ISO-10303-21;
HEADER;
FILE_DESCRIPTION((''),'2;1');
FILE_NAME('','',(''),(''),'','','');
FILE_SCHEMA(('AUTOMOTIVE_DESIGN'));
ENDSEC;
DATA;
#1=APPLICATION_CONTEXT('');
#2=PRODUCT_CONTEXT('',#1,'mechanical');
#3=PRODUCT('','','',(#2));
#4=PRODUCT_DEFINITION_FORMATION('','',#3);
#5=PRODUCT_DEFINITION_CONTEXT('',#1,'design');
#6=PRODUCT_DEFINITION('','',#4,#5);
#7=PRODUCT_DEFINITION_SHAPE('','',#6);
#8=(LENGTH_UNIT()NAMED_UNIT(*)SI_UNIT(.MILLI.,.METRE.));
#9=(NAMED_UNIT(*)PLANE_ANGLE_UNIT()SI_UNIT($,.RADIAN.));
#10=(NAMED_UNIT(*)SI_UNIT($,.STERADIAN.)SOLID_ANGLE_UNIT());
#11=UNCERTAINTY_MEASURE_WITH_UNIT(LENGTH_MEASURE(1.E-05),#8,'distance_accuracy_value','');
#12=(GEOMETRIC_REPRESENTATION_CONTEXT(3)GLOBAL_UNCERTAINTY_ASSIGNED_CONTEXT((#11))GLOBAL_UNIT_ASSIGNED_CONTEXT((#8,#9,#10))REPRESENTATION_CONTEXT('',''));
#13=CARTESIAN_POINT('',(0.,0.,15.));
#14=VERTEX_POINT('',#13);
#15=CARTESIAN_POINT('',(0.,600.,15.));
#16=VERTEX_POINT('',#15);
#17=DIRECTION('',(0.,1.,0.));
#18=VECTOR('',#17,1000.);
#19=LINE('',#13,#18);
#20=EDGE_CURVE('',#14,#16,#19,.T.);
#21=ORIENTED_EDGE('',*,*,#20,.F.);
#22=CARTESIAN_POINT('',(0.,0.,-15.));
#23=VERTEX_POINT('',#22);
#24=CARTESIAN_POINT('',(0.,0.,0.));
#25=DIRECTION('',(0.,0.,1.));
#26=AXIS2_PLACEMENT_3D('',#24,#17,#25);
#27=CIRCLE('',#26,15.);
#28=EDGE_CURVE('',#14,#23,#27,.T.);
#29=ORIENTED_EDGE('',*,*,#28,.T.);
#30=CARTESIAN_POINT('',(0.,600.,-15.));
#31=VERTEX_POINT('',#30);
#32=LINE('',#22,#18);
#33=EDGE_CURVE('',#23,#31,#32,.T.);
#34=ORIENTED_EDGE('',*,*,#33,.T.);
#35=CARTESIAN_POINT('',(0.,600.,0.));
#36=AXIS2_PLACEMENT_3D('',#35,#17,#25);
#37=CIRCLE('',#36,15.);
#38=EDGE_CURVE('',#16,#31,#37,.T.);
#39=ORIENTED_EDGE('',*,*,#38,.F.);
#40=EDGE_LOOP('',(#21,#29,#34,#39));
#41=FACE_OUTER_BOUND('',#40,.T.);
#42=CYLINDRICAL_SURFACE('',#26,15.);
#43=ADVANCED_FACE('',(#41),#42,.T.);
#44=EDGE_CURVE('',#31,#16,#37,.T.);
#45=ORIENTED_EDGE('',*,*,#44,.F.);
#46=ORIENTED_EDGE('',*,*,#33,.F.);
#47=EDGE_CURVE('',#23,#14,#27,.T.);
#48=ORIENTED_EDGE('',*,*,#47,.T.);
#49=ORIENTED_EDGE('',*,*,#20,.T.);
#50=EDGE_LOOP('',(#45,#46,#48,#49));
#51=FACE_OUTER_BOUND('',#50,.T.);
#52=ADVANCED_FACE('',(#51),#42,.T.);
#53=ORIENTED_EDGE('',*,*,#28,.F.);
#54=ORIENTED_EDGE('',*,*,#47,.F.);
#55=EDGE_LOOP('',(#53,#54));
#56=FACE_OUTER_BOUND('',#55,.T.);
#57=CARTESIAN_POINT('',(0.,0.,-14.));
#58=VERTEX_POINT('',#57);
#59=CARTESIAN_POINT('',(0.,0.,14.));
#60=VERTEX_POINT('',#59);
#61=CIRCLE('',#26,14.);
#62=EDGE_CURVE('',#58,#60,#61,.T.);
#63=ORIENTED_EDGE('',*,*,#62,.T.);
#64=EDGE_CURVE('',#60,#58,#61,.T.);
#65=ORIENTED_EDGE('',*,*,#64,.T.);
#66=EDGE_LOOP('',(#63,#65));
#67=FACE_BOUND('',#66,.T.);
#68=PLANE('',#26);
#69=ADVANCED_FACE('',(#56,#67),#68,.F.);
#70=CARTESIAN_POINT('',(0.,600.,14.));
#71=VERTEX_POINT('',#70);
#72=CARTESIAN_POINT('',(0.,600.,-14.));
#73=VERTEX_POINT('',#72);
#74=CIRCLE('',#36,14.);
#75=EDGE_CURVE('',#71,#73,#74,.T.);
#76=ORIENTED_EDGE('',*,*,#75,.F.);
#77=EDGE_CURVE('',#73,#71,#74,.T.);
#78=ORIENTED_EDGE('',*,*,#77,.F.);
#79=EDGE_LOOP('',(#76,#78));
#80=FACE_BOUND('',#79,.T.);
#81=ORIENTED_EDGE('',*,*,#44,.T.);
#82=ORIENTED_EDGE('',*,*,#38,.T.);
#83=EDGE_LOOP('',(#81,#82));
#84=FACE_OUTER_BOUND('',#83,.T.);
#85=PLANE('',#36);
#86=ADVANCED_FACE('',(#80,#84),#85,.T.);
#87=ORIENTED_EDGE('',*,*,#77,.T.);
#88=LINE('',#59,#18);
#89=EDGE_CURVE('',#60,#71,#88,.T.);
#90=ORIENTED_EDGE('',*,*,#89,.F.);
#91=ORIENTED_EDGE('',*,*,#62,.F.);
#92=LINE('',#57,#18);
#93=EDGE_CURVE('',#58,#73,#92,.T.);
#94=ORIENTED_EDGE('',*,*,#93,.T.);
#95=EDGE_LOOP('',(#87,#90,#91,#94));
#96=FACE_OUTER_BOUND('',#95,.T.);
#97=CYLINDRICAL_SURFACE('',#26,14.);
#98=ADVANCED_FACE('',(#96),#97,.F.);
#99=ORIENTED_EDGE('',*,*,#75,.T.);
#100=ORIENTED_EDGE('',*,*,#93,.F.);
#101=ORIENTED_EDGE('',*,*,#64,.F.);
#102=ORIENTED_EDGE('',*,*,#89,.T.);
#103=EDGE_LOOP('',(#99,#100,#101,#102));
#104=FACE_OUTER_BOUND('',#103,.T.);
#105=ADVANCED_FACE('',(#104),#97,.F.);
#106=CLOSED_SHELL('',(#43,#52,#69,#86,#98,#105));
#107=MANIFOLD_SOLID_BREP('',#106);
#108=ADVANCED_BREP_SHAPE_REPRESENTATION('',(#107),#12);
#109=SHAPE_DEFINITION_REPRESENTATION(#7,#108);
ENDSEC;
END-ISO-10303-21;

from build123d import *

# Parameters (mm, degrees)
SWEEP_THIN1_PROFILE_R   = 15
SWEEP_THIN1_PROFILE_R_2 = 14


with BuildPart() as part:
    # Sweep-Thin1: sweep along a path in Sketch1
    with BuildLine(Plane.XY) as sweep_thin1_path:
        Line((0, 0), (0, 600))
    # Sweep-Thin1 profile (on start of the path) → Sweep-Thin1 (sweep)
    with BuildSketch(Plane.ZX):
        Circle(SWEEP_THIN1_PROFILE_R)
        Circle(SWEEP_THIN1_PROFILE_R_2, mode=Mode.SUBTRACT)
    sweep(path=sweep_thin1_path.line)


solid = part.part
